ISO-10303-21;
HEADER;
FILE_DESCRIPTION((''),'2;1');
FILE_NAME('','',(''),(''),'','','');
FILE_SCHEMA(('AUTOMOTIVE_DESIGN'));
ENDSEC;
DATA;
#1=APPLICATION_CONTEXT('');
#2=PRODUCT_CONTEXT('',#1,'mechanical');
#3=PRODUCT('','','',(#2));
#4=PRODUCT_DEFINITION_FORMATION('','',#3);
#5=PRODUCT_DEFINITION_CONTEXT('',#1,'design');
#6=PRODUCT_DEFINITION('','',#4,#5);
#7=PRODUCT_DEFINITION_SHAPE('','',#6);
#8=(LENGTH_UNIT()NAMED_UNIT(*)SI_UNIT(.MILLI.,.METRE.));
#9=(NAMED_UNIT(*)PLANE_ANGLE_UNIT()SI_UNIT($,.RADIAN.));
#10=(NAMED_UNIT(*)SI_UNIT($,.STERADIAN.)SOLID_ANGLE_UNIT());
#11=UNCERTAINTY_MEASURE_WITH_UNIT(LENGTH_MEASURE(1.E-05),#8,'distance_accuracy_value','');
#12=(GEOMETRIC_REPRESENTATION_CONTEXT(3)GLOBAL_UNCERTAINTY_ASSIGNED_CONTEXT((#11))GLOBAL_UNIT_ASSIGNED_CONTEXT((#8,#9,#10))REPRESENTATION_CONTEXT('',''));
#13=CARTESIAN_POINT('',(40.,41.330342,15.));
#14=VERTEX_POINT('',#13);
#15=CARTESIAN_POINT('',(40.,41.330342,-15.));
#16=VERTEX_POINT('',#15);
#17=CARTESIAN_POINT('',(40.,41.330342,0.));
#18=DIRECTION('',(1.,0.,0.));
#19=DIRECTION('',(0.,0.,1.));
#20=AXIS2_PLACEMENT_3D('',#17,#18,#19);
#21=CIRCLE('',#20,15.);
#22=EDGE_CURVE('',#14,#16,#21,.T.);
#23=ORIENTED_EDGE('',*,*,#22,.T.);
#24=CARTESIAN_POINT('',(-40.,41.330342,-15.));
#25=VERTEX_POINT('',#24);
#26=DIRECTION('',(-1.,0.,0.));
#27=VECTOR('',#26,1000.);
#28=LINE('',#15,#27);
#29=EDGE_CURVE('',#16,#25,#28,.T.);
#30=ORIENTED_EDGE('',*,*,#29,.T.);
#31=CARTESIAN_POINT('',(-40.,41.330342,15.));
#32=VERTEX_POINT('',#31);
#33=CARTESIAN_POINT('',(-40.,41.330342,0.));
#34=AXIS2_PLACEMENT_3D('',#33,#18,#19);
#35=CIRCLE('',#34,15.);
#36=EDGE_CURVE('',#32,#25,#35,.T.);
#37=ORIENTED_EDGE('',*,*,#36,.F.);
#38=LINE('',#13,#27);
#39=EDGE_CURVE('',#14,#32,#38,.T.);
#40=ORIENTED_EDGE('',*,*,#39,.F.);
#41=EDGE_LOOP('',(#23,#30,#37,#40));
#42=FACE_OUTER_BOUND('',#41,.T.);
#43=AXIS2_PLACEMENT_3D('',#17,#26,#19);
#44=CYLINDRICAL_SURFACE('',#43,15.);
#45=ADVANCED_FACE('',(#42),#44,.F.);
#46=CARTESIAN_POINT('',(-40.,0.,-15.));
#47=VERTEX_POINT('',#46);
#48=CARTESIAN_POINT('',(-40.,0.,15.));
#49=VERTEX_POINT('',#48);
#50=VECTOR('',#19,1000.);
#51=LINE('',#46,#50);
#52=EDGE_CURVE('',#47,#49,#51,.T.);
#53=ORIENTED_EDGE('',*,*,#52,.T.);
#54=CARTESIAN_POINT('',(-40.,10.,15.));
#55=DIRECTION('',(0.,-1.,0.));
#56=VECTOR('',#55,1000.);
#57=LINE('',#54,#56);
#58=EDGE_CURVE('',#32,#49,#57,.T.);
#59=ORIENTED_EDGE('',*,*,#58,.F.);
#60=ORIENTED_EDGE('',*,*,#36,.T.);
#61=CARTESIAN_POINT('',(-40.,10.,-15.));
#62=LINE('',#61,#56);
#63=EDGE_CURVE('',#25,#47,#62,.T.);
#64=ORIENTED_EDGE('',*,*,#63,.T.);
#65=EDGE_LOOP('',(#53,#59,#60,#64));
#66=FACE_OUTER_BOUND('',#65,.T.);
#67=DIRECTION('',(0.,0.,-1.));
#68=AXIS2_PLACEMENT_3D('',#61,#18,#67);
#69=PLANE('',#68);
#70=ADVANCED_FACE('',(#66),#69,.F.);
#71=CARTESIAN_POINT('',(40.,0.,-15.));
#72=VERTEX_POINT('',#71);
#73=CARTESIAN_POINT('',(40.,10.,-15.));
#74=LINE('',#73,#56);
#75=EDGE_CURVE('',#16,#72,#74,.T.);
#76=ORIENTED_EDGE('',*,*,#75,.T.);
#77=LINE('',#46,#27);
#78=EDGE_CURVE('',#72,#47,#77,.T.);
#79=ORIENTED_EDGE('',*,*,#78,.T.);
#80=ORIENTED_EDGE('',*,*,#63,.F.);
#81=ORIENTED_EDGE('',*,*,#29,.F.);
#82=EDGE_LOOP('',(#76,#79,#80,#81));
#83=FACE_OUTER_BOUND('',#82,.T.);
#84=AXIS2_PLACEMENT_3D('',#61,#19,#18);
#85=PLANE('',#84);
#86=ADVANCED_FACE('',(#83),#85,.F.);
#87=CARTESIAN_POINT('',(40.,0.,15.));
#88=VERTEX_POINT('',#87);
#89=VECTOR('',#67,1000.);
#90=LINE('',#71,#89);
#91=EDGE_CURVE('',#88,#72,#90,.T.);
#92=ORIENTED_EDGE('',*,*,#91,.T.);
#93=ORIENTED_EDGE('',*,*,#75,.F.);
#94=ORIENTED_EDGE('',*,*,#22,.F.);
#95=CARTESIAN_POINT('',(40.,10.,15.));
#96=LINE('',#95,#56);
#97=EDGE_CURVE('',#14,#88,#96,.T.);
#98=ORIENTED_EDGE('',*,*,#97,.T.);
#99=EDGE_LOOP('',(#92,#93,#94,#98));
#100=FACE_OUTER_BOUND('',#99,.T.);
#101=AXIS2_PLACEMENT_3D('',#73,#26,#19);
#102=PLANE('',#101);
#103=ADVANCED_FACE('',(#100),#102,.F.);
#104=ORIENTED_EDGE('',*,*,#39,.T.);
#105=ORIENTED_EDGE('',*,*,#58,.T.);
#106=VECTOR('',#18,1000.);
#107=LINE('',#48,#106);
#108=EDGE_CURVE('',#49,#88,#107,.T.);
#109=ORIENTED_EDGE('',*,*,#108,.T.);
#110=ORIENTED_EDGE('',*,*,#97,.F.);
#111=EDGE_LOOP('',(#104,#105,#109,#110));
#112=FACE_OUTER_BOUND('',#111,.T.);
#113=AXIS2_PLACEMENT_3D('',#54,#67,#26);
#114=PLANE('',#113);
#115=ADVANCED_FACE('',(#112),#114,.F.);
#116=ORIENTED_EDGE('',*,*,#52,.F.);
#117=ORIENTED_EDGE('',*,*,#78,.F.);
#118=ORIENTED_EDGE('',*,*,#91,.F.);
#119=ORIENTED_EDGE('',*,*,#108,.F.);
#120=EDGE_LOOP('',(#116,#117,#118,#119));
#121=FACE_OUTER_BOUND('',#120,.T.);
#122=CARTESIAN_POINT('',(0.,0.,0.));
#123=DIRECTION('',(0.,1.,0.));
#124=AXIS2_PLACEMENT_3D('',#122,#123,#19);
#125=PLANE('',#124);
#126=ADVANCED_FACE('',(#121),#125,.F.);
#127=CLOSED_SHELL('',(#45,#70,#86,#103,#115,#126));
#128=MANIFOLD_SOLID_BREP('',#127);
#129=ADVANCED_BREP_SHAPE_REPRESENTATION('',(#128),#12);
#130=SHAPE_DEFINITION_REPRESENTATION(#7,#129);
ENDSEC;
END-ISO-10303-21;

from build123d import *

# Parameters (mm, degrees)
SKETCH1_W           = 80
SKETCH1_H           = 30
BOSS_EXTRUDE1_DEPTH = 10
BOSS_EXTRUDE2_DEPTH = 80


with BuildPart() as part:
    # Sketch1 → Boss-Extrude1 (new body)
    with BuildSketch(Plane(origin=(0, 0, 0), x_dir=(1, 0, 0), z_dir=(0, 1, 0))):
        Rectangle(SKETCH1_W, SKETCH1_H)
    extrude(amount=BOSS_EXTRUDE1_DEPTH)

    # Sketch3 → Boss-Extrude2 (add)
    with BuildSketch(Plane.ZY.offset(40)):
        with BuildLine():
            Line((-15, 10), (-15, 41.330342273))
            ThreePointArc((-15, 41.330342273), (0, 26.330342273), (15, 41.330342273))
            Line((15, 41.330342273), (15, 10))
            Line((15, 10), (-15, 10))
        make_face()
    extrude(amount=-BOSS_EXTRUDE2_DEPTH)


solid = part.part
